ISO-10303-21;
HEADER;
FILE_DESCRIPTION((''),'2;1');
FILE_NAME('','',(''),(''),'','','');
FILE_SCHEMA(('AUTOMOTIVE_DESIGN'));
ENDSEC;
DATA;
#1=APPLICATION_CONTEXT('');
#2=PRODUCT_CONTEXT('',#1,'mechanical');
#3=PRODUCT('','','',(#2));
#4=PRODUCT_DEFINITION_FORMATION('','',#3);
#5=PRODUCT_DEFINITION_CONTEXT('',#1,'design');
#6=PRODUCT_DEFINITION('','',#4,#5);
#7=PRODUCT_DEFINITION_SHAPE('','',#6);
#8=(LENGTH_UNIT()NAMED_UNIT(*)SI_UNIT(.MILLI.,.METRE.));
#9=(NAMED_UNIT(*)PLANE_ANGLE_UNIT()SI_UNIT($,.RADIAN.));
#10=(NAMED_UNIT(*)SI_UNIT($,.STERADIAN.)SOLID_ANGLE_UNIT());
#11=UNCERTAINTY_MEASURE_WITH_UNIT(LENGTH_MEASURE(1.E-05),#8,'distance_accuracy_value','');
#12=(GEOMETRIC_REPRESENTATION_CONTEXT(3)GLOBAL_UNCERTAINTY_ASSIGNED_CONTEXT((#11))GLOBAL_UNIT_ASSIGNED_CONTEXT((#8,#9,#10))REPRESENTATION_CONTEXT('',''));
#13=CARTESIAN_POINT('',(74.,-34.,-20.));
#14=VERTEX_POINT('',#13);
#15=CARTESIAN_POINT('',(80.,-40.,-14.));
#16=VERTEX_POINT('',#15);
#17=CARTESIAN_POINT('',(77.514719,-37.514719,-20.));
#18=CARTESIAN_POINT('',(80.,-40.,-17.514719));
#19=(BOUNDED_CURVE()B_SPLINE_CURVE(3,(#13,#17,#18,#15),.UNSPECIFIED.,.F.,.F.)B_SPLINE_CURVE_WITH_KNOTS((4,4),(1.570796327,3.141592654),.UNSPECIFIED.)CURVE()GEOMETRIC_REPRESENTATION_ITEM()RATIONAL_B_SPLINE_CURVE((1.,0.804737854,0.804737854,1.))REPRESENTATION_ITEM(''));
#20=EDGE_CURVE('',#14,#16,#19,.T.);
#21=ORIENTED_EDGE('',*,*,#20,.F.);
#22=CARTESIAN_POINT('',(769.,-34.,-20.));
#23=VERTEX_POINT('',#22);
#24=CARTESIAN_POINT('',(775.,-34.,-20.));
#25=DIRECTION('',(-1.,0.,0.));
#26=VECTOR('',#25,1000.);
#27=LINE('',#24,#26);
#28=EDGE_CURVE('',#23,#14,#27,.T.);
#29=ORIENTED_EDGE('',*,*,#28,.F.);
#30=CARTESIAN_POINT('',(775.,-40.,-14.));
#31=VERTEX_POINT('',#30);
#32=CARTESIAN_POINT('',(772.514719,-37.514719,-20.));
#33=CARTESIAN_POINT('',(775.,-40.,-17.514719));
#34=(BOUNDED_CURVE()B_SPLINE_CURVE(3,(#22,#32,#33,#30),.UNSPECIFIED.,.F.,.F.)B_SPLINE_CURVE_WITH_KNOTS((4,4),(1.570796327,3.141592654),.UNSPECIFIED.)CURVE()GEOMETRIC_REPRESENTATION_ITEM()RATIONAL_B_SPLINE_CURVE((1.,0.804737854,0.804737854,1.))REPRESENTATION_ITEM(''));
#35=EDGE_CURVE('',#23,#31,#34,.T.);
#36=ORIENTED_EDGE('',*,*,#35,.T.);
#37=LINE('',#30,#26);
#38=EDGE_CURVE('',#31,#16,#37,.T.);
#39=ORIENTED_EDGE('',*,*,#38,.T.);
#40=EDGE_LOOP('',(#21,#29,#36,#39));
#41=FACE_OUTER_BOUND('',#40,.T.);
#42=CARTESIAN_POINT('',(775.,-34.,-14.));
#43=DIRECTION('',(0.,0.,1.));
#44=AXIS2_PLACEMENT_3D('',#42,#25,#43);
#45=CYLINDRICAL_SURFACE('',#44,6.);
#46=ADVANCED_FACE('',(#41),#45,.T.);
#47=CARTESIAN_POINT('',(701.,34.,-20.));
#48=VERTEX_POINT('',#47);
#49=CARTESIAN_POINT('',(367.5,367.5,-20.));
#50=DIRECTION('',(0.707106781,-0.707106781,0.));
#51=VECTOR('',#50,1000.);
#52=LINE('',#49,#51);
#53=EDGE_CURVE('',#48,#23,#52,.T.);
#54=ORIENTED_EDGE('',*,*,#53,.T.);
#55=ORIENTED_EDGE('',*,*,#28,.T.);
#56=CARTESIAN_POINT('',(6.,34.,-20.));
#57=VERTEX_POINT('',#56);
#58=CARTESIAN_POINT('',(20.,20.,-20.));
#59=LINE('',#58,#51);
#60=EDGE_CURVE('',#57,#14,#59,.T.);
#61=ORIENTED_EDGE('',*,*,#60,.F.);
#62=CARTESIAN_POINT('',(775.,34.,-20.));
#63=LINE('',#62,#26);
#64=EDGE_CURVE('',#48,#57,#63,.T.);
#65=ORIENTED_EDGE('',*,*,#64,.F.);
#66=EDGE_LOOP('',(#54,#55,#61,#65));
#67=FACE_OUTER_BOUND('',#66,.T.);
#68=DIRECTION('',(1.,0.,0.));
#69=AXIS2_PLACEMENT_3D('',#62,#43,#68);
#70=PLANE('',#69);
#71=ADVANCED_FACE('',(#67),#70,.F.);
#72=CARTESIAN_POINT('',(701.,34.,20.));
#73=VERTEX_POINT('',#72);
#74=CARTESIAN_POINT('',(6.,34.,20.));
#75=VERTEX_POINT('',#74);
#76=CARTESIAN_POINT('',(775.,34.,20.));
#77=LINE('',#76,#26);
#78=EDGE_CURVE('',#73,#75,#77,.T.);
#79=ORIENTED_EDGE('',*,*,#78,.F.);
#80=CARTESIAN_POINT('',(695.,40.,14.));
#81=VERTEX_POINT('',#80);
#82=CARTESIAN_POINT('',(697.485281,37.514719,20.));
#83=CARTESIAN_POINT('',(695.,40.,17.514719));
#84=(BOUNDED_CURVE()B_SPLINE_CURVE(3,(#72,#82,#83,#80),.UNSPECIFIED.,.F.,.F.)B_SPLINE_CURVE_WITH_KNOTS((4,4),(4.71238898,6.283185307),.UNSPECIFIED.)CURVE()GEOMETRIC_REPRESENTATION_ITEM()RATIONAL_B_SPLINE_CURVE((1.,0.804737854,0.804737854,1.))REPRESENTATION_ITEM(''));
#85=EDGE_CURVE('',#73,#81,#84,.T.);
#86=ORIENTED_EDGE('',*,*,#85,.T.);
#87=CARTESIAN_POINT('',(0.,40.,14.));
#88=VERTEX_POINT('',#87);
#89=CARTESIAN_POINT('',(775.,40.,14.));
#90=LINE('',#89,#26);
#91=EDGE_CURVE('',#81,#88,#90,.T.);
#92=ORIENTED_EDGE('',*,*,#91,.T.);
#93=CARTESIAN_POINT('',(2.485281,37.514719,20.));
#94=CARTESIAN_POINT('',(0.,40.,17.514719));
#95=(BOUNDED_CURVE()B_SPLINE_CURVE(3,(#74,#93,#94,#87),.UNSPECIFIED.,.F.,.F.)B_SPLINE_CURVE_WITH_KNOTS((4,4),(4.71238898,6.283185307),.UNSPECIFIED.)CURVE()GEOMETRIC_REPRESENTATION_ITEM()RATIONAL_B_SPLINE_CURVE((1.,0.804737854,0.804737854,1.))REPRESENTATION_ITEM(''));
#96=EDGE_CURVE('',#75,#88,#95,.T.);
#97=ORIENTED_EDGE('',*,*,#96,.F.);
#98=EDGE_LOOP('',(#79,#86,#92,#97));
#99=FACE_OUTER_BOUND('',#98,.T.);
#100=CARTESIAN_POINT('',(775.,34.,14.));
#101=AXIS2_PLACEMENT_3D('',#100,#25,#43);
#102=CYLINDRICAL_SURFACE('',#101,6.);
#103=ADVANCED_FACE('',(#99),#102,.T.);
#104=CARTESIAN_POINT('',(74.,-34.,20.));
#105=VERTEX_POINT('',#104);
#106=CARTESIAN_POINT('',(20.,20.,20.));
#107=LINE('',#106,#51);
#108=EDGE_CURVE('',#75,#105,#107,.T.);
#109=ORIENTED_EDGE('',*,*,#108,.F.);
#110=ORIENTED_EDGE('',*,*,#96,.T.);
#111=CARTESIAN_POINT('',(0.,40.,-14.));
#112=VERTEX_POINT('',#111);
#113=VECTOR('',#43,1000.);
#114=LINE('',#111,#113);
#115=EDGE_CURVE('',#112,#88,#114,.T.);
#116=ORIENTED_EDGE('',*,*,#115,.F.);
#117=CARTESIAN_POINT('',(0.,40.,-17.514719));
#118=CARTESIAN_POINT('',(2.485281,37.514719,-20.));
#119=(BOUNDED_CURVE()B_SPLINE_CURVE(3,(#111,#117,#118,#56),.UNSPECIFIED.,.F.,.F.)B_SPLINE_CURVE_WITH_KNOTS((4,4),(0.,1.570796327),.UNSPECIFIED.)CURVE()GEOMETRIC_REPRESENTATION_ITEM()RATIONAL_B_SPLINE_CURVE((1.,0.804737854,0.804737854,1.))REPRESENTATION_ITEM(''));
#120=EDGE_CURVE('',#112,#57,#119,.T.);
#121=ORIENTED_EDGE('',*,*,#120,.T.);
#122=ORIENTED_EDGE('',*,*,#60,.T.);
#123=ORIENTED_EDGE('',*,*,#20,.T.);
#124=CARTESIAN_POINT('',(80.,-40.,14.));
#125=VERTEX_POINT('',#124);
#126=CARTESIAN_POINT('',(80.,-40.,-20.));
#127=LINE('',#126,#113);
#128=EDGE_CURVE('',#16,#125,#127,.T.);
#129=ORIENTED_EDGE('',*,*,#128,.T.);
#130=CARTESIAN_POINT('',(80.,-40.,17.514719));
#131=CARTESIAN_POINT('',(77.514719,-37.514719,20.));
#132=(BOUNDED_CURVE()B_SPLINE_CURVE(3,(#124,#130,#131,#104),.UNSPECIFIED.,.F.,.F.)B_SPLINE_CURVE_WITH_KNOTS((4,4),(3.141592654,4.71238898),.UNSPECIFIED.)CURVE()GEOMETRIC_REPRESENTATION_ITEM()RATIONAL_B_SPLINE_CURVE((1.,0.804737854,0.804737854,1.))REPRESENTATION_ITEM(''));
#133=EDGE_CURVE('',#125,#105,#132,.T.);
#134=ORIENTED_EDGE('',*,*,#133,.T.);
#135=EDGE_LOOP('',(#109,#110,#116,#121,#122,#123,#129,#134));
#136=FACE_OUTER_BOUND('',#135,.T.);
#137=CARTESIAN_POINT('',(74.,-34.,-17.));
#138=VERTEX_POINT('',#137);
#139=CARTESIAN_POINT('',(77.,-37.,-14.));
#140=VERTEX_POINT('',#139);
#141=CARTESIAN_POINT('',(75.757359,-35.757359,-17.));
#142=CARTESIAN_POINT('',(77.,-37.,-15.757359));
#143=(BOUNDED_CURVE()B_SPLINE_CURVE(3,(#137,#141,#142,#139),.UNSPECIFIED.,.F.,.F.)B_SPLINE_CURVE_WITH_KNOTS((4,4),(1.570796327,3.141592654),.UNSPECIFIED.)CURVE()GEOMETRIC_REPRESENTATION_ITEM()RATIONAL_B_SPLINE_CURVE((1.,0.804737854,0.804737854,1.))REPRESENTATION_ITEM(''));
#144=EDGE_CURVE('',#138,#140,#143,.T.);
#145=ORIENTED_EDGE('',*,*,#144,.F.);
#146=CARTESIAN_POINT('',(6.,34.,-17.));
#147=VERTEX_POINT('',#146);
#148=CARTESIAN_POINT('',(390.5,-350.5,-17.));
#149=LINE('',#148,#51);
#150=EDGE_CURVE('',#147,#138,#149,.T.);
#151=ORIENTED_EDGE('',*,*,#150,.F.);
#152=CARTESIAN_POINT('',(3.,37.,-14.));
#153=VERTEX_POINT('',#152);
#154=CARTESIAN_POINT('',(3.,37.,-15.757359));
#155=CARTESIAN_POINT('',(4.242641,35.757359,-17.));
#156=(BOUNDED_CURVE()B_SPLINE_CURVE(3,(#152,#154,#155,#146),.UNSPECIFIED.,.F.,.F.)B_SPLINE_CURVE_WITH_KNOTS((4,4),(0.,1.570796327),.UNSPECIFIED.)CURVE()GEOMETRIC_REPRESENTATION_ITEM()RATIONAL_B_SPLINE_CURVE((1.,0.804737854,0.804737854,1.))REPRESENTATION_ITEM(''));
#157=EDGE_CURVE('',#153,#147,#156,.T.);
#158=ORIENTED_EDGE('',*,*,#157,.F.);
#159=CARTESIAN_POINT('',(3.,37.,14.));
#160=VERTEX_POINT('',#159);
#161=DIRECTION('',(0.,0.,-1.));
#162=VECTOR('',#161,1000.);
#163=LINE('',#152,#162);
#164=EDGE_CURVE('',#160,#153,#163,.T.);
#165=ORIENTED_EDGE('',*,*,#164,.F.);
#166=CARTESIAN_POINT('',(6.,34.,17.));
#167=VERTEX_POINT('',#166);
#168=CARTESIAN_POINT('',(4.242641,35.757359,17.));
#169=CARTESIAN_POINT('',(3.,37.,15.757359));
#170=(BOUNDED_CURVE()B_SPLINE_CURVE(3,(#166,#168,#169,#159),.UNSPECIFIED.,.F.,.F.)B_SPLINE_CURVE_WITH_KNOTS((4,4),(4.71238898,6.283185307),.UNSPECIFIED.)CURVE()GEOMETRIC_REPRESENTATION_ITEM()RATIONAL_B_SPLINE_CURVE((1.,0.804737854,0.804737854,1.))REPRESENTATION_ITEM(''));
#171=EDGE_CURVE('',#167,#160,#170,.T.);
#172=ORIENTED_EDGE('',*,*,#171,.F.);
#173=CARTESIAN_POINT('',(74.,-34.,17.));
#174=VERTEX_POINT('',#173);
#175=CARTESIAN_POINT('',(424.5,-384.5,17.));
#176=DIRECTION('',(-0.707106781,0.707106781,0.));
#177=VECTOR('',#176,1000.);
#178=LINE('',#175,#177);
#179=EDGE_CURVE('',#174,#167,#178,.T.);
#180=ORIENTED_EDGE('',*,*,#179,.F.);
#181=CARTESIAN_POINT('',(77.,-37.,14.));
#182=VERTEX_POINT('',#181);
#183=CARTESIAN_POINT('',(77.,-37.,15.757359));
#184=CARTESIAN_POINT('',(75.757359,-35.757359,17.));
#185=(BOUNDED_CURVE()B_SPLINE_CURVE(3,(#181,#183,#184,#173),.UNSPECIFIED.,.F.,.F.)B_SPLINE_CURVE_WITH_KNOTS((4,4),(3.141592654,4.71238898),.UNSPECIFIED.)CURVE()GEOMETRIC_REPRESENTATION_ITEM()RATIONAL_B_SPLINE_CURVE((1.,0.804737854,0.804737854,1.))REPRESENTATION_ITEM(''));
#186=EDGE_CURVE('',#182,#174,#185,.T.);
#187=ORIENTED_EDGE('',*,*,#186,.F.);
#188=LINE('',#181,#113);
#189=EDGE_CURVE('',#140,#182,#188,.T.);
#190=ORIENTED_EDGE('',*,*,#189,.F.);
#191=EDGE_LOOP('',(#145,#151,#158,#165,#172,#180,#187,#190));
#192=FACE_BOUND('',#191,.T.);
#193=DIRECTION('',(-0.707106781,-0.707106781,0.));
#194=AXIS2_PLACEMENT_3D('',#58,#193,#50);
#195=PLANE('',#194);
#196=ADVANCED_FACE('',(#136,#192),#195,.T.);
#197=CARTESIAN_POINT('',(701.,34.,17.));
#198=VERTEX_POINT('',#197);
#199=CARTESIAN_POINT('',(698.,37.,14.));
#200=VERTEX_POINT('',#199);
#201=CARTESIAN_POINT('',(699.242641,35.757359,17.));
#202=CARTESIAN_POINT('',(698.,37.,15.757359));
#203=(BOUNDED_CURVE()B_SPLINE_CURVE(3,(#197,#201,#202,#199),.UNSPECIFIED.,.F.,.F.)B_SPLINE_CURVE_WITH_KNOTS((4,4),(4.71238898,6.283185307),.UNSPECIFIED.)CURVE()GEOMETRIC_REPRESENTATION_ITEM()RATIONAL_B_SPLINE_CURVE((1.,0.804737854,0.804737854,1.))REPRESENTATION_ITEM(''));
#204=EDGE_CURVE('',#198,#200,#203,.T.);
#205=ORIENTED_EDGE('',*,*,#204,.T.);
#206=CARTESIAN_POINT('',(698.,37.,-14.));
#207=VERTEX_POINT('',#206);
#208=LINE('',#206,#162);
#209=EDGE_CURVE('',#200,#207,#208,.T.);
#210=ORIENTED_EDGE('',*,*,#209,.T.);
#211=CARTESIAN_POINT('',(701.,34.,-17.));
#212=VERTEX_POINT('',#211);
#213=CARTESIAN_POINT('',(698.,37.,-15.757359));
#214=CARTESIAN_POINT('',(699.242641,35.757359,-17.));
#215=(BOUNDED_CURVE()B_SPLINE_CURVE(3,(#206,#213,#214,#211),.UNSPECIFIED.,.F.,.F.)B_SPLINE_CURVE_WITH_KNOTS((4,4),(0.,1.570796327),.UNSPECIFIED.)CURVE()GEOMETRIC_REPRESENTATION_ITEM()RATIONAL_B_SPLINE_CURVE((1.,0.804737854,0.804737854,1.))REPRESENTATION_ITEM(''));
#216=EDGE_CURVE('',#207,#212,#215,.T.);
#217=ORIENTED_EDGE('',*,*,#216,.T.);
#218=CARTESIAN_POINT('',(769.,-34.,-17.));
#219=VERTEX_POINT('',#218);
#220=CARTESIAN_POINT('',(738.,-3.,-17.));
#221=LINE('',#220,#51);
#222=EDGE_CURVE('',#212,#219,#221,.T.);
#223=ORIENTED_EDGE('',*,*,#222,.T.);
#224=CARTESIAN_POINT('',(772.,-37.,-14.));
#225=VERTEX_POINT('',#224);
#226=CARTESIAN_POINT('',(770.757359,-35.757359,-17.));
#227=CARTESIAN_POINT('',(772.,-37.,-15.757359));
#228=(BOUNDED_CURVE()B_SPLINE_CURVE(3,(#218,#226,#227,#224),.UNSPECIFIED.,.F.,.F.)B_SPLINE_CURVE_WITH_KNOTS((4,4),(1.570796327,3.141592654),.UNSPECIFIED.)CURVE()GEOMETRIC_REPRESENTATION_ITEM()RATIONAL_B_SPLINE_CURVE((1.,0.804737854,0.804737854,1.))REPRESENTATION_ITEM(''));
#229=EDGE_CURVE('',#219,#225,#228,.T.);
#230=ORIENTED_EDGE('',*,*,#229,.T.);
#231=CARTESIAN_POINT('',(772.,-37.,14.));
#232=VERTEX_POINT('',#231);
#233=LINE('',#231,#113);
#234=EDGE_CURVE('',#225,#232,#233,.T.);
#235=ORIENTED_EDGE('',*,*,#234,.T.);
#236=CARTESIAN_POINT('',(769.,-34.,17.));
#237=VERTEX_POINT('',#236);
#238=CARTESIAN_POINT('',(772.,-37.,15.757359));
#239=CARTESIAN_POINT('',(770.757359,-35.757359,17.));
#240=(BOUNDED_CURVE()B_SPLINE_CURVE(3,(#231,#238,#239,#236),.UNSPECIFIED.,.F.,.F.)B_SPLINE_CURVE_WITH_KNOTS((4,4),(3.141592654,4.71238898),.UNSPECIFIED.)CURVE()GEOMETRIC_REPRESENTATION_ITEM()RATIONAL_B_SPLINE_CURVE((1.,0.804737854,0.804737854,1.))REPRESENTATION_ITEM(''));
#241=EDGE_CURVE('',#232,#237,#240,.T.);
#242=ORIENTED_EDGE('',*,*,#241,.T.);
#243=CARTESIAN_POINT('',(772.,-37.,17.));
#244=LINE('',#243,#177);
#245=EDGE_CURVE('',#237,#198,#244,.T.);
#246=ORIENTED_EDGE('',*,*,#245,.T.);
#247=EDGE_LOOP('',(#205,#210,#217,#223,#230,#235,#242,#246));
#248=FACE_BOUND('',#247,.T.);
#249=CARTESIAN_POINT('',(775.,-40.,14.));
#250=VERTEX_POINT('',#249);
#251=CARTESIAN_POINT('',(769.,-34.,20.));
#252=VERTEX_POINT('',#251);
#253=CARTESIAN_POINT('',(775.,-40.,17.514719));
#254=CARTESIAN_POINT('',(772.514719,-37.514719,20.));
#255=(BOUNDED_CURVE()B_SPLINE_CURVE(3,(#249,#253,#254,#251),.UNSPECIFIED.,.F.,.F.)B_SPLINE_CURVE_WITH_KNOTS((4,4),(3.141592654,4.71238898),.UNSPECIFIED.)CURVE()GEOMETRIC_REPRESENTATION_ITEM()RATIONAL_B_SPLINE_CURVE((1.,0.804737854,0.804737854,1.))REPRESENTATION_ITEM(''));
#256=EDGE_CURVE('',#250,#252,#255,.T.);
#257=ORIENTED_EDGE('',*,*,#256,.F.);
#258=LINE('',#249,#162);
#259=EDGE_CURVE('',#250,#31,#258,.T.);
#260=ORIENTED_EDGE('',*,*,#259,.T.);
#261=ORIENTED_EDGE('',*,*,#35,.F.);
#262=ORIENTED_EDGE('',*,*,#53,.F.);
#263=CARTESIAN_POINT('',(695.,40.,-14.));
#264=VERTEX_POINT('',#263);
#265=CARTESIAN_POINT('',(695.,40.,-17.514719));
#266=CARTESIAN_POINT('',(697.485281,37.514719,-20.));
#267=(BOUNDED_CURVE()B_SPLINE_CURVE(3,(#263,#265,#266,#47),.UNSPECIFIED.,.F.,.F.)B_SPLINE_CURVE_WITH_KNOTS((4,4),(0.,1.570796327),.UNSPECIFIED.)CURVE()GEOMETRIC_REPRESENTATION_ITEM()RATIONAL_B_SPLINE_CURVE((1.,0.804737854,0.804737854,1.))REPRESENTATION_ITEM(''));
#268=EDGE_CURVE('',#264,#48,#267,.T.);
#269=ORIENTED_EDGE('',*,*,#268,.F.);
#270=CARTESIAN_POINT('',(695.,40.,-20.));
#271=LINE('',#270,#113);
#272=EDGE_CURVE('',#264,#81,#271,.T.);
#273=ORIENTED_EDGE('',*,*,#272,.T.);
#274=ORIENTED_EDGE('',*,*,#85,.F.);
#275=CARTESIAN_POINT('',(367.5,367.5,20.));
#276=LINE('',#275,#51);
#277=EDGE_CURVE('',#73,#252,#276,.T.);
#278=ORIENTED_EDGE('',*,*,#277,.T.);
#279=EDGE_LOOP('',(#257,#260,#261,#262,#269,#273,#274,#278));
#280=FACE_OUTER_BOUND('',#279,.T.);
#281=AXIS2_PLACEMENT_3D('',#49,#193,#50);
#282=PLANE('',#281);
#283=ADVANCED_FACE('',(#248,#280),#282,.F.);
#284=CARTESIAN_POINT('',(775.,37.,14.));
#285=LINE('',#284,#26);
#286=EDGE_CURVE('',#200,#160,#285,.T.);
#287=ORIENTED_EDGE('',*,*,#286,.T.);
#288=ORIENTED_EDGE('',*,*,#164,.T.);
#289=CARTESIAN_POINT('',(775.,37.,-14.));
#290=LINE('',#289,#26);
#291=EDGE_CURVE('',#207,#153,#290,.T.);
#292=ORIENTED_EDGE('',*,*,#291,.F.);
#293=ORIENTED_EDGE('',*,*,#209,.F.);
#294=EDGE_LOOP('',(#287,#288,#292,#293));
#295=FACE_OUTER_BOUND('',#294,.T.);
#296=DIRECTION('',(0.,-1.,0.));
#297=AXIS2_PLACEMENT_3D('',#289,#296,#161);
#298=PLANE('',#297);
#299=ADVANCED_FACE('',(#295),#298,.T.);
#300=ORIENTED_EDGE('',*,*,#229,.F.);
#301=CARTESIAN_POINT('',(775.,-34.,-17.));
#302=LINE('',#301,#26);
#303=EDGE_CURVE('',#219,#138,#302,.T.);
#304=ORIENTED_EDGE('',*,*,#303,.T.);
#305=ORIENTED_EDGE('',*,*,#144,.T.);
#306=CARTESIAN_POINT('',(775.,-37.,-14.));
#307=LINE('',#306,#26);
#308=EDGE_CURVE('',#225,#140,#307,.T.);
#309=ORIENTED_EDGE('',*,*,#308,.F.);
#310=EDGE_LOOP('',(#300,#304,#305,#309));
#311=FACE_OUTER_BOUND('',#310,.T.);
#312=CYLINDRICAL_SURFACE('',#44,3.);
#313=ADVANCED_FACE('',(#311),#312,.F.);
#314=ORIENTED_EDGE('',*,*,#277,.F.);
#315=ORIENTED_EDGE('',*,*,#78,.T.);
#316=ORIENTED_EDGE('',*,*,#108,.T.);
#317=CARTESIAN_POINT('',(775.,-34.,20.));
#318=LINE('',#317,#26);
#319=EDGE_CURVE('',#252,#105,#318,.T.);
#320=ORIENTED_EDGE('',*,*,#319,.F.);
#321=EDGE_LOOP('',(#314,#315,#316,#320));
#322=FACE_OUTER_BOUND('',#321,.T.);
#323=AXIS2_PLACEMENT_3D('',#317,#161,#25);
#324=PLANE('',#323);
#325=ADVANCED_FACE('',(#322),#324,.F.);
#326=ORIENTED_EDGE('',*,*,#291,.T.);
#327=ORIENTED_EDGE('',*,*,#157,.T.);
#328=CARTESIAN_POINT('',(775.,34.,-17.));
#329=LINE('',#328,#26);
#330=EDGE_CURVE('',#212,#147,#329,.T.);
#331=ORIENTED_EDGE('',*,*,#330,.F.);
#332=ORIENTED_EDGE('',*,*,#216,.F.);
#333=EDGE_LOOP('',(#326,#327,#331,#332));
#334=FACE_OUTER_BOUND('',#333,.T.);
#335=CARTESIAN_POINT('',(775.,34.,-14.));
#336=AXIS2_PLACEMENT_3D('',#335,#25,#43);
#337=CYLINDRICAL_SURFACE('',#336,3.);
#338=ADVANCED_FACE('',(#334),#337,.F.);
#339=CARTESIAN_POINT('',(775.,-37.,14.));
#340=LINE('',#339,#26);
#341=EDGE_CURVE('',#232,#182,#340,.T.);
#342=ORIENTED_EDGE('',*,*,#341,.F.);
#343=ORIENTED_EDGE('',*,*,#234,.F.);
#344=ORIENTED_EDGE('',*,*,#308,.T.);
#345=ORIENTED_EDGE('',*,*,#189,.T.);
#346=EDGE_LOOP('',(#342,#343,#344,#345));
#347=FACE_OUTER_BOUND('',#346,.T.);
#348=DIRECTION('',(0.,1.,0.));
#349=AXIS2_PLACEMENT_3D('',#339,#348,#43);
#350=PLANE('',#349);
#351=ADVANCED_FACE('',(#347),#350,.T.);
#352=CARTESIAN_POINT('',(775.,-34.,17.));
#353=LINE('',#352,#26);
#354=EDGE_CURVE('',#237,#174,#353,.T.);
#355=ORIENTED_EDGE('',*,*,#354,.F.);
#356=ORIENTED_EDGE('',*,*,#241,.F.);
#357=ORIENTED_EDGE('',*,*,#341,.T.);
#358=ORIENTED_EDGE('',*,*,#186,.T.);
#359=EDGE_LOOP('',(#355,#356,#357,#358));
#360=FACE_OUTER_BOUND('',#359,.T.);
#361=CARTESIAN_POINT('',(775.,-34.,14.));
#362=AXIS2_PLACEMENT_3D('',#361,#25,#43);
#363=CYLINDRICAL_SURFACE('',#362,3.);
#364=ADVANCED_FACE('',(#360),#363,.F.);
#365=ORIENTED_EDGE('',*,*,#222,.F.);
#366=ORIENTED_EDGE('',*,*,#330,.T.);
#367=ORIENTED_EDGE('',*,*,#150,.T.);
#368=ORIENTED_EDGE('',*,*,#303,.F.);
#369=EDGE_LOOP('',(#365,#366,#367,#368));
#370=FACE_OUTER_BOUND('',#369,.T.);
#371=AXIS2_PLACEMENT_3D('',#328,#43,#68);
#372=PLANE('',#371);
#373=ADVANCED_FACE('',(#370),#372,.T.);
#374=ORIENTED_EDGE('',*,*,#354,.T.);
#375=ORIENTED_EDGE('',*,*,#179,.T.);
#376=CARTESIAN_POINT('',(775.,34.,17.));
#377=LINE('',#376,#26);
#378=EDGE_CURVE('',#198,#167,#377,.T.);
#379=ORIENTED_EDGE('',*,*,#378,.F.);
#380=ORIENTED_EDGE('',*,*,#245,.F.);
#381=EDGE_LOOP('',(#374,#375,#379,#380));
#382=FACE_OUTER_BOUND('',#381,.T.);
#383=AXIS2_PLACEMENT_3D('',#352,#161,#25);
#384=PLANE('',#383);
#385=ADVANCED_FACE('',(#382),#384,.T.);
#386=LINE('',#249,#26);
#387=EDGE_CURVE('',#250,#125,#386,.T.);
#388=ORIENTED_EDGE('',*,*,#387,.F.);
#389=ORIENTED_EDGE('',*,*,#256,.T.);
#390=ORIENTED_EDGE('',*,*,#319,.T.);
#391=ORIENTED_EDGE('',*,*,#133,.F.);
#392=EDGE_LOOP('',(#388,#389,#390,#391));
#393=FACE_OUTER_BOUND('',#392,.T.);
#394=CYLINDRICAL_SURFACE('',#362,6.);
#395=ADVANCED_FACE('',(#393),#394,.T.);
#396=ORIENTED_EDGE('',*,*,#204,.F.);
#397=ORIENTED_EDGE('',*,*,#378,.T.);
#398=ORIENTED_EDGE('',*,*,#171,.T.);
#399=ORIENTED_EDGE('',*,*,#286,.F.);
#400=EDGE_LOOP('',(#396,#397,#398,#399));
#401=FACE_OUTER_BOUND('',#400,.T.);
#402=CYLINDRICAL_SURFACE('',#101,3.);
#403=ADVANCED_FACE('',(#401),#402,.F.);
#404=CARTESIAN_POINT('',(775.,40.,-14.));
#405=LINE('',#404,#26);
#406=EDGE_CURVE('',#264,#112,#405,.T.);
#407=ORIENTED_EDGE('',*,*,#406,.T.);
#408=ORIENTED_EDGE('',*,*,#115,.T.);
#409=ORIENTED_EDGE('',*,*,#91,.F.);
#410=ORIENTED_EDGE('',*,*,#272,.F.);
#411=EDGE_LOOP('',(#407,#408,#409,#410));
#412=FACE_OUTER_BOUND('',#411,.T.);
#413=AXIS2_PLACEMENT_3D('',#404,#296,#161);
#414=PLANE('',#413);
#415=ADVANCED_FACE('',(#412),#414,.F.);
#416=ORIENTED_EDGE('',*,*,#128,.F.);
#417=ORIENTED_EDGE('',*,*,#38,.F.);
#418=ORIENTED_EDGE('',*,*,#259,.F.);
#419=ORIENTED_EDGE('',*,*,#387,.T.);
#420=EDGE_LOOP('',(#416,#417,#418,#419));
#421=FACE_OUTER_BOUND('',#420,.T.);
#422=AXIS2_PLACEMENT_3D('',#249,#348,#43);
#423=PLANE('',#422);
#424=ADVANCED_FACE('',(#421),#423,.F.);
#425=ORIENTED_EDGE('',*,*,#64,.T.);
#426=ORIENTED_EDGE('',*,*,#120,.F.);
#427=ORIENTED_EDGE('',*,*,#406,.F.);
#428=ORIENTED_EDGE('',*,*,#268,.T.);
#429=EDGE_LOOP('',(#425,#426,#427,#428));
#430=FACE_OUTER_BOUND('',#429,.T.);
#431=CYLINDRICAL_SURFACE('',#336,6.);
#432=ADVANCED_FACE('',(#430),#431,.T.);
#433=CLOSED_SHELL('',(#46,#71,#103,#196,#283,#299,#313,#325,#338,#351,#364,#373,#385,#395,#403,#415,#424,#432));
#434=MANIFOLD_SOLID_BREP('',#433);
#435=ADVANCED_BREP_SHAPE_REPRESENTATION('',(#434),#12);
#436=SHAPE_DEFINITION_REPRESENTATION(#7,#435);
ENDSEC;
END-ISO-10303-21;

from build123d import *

# Parameters (mm, degrees)
COLD_FORMED_RECT_HOLLOW_SECTION_GB_T_672_DEPTH = 775
CUT_EXTRUDE1_DEPTH                             = 778.061773606


with BuildPart() as part:
    # Sketch1 → Cold-Formed Rect Hollow Section GB/T 6728-2002 80 X 40 X 3(1) (new body)
    with BuildSketch(Plane(origin=(0, 0, 0), x_dir=(0, 0, -1), z_dir=(1, 0, 0))):
        with BuildLine():
            Line((-14, -40), (14, -40))
            ThreePointArc((14, -40), (18.242640687, -38.242640687), (20, -34))
            Line((20, -34), (20, 34))
            ThreePointArc((20, 34), (18.242640687, 38.242640687), (14, 40))
            Line((14, 40), (-14, 40))
            ThreePointArc((-14, 40), (-18.242640687, 38.242640687), (-20, 34))
            Line((-20, 34), (-20, -34))
            ThreePointArc((-20, -34), (-18.242640687, -38.242640687), (-14, -40))
        make_face()
        with BuildLine():
            Line((-14, -37), (14, -37))
            ThreePointArc((14, -37), (16.121320344, -36.121320344), (17, -34))
            Line((17, -34), (17, 34))
            ThreePointArc((17, 34), (16.121320344, 36.121320344), (14, 37))
            Line((14, 37), (-14, 37))
            ThreePointArc((-14, 37), (-16.121320344, 36.121320344), (-17, 34))
            Line((-17, 34), (-17, -34))
            ThreePointArc((-17, -34), (-16.121320344, -36.121320344), (-14, -37))
        make_face(mode=Mode.SUBTRACT)
    extrude(amount=COLD_FORMED_RECT_HOLLOW_SECTION_GB_T_672_DEPTH)

    # Sketch2 → Cut-Extrude1 (cut, through all)
    with BuildSketch(Plane.XY.offset(20)):
        Polygon((0, 40), (80, -40), (0, -40), (0, -34), (0, 34), align=None)
        Polygon((775, 40), (695, 40), (775, -40), align=None)
    extrude(amount=-CUT_EXTRUDE1_DEPTH, mode=Mode.SUBTRACT)


solid = part.part
